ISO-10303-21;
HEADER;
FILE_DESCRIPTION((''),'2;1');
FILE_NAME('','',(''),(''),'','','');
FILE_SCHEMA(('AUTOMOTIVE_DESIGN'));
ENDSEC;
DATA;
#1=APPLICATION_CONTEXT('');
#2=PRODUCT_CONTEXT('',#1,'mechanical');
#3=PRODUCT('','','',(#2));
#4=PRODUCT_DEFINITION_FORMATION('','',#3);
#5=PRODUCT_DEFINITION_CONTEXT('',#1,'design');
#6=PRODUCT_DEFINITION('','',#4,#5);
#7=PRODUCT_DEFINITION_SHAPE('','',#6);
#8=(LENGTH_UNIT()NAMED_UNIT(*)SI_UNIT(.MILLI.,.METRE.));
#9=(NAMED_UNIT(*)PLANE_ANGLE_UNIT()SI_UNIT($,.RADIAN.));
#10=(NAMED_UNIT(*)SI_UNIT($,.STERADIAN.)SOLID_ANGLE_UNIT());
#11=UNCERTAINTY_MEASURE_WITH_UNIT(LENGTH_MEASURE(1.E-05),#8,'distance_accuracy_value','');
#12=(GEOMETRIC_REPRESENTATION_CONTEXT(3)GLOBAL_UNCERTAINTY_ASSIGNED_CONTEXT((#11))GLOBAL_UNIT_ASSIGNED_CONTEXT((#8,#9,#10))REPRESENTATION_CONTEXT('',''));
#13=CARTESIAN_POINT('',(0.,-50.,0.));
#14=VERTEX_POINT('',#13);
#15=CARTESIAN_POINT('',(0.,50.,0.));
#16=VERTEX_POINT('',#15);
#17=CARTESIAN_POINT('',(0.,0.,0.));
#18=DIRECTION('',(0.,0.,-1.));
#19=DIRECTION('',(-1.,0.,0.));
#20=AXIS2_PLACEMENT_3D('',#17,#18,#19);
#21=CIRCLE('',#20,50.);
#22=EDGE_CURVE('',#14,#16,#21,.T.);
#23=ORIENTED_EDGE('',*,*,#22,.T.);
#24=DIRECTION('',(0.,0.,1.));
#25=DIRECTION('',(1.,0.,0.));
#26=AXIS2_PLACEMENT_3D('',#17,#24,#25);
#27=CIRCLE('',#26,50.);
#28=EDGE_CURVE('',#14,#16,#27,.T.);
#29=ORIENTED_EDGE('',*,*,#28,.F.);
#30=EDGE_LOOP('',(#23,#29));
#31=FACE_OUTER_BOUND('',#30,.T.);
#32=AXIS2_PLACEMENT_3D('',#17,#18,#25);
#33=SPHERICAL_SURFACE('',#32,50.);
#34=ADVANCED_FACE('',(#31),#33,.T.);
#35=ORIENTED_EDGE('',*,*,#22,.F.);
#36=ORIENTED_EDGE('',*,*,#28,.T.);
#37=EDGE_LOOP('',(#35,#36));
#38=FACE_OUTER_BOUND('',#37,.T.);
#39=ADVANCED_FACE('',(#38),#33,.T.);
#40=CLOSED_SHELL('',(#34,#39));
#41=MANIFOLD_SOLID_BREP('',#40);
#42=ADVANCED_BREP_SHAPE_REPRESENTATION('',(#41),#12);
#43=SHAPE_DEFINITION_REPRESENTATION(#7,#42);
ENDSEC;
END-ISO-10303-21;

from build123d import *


with BuildPart() as part:
    # 草图1 → 旋转1 (revolve)
    with BuildSketch(Plane.XY):
        with BuildLine():
            Line((0, 50), (0, -50))
            ThreePointArc((0, -50), (50, 0), (0, 50))
        make_face()
    revolve(axis=Axis((0, 50, 0), (0, -1, 0)))


solid = part.part
